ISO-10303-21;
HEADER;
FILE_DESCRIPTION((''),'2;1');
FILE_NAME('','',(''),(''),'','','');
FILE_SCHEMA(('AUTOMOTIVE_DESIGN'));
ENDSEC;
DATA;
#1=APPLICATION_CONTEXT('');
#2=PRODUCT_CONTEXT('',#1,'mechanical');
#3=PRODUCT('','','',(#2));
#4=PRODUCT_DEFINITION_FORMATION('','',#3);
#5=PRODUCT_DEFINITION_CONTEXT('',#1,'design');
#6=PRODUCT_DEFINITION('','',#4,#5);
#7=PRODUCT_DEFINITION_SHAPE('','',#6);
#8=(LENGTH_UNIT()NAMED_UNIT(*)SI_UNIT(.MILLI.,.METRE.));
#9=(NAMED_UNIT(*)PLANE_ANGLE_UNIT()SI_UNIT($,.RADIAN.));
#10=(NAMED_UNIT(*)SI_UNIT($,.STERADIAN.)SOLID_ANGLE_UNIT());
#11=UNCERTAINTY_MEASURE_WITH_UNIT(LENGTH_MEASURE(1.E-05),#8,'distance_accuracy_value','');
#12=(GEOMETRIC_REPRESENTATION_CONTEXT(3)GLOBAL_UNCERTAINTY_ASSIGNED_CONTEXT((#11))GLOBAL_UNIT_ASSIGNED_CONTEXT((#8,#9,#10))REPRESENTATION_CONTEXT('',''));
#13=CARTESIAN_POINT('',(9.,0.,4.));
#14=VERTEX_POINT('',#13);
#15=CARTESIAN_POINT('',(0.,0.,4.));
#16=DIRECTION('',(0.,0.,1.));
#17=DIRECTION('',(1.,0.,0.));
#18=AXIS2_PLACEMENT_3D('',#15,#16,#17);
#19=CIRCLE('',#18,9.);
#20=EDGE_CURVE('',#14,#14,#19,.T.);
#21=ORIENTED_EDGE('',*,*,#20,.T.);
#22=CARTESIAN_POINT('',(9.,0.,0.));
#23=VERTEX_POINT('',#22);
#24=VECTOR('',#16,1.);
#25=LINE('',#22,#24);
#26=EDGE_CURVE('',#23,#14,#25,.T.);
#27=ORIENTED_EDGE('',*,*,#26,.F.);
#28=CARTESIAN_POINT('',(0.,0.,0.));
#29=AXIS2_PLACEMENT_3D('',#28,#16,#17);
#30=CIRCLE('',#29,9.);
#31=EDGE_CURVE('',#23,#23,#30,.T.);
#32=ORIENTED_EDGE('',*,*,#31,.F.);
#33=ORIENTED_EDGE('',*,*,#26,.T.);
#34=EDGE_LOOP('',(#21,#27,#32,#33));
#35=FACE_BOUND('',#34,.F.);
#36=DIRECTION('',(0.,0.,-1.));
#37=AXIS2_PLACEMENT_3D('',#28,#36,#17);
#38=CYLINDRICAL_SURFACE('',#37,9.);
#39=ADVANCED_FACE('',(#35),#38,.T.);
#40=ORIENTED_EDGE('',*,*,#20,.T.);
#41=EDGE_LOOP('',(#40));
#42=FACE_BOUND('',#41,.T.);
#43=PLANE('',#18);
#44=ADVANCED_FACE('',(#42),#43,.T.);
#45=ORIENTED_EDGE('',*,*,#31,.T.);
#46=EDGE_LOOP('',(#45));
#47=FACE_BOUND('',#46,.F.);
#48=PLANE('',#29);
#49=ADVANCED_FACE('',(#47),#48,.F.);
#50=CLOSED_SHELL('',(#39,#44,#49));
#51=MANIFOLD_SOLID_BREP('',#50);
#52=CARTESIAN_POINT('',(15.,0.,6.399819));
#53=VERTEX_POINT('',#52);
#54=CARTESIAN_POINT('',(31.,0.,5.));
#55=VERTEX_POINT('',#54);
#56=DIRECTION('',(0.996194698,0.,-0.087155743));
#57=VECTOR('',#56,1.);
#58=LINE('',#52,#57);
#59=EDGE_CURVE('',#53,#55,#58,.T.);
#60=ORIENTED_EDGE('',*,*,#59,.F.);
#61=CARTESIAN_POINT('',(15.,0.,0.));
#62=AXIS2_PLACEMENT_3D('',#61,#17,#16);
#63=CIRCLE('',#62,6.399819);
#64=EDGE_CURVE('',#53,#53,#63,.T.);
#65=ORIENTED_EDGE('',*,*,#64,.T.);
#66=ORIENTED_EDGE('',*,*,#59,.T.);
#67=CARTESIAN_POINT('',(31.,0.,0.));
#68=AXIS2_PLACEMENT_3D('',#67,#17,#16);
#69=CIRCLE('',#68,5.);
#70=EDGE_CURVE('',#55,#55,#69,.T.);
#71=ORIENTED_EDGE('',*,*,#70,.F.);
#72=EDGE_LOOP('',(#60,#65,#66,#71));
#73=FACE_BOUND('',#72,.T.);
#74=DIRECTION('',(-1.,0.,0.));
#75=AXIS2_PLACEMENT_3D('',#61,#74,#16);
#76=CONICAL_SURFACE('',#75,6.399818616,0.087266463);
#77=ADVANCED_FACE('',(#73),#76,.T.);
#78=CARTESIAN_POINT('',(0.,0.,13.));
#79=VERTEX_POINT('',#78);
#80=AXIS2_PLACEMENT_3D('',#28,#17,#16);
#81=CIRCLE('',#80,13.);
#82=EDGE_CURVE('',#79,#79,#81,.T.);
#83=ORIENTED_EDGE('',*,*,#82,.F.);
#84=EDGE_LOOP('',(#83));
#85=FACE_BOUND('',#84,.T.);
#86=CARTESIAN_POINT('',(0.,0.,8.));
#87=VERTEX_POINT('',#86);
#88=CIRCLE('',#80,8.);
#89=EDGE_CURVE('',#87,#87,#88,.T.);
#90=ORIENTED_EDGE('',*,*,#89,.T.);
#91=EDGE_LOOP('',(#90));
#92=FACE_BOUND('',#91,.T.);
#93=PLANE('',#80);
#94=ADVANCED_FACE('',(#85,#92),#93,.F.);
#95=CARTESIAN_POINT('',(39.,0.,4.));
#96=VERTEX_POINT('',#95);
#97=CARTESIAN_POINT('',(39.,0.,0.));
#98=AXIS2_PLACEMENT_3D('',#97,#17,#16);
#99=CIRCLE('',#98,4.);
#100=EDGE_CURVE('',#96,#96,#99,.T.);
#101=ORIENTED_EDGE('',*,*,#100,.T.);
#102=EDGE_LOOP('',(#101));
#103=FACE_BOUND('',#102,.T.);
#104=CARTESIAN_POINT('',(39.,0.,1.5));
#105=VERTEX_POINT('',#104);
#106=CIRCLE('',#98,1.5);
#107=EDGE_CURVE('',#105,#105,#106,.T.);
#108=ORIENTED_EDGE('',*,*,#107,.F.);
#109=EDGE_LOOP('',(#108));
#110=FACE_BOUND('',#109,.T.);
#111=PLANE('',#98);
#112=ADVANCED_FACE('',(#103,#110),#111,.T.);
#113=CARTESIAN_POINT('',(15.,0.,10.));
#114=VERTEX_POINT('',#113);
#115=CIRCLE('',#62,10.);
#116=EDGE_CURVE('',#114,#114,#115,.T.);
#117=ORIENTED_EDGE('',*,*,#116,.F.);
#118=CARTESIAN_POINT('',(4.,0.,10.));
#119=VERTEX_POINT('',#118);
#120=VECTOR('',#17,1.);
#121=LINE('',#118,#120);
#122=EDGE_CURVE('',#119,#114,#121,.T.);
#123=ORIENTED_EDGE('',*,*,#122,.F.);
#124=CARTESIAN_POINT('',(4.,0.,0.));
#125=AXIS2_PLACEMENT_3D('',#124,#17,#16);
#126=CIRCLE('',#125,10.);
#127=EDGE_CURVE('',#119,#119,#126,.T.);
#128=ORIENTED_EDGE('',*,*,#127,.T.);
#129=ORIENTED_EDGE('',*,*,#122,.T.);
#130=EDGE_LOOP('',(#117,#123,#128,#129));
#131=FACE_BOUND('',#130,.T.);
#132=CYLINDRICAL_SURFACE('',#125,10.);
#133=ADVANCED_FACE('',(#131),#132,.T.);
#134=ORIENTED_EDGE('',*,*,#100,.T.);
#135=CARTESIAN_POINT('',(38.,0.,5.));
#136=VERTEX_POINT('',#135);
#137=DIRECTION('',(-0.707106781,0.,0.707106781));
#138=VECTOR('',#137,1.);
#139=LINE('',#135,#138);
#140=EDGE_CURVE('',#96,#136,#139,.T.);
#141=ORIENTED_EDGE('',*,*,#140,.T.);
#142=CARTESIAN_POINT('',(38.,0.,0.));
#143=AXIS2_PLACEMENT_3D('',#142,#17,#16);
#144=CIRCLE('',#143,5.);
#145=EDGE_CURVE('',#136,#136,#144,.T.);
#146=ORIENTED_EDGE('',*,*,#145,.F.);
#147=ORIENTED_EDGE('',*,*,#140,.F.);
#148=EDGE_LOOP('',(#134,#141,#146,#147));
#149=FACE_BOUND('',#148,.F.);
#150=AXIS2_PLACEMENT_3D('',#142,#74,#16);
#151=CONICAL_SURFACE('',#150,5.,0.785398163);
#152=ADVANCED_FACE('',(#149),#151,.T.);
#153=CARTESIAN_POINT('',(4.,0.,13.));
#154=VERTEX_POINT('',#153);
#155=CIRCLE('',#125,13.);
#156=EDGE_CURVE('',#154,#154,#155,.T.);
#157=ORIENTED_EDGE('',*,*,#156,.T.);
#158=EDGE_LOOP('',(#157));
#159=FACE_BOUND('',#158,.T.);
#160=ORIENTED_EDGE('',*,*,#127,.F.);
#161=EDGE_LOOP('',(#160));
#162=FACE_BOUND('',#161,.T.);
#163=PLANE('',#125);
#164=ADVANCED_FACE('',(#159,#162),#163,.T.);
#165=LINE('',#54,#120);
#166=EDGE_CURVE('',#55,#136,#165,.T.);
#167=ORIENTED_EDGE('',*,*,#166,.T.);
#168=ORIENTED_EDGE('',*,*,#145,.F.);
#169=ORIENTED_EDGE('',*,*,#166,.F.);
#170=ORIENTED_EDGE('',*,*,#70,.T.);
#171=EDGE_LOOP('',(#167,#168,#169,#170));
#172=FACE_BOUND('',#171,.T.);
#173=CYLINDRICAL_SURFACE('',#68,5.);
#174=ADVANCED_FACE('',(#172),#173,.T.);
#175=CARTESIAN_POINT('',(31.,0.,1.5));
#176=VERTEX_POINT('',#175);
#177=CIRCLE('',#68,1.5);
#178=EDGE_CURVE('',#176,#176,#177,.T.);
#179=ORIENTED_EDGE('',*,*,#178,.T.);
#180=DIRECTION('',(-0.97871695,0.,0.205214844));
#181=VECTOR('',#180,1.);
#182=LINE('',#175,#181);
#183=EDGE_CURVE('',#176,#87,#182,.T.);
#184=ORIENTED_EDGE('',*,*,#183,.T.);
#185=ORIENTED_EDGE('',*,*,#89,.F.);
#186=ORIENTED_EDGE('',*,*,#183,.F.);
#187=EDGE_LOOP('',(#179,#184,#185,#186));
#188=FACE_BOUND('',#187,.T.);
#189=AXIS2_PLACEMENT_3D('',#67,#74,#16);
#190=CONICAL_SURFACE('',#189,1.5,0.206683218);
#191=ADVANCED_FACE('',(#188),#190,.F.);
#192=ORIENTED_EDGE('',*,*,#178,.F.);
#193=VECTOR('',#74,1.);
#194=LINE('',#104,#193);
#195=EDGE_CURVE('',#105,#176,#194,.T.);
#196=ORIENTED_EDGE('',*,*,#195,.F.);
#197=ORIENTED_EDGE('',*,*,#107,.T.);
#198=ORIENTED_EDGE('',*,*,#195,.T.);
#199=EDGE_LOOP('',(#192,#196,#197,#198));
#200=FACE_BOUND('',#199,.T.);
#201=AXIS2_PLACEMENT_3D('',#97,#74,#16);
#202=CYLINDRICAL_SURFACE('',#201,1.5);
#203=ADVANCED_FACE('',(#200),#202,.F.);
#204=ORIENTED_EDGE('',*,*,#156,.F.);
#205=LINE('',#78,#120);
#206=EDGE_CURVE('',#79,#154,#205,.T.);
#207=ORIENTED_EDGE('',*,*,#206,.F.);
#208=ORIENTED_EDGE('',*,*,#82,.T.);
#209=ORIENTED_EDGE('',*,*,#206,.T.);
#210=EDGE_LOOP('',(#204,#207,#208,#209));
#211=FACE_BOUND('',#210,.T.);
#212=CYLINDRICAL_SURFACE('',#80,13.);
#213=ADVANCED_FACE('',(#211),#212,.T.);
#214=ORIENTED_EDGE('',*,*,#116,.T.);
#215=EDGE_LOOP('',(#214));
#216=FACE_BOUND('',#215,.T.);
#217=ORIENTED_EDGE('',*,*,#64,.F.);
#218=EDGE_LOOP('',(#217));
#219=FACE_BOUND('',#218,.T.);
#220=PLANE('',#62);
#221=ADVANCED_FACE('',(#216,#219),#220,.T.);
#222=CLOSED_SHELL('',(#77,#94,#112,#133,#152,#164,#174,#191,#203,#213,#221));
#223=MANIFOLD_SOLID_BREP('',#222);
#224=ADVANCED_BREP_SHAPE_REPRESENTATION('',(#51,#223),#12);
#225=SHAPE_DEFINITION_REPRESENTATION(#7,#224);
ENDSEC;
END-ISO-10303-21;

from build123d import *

# Parameters (mm, degrees)
SKETCH8_R           = 9
BOSS_EXTRUDE3_DEPTH = 4
CHAMFER1_SIZE       = 1


with BuildPart() as part:
    # Sketch8 → Boss-Extrude3 (new body)
    with BuildSketch(Plane.XY):
        Circle(SKETCH8_R)
    extrude(amount=BOSS_EXTRUDE3_DEPTH)


with BuildPart() as body_2:
    # Sketch10 → Revolve1 (revolve)
    with BuildSketch(Plane(origin=(0, 0, 0), x_dir=(1, 0, 0), z_dir=(0, 1, 0)), mode=Mode.PRIVATE) as revolve1_sk:
        Polygon((0, 0), (0, 13), (4, 13), (4, 10), (15, 10), (15, 6.399818616), (31, 5), (39, 5), (39, 0), align=None)
    revolve(revolve1_sk.sketch.rotate(Axis((0, 0, 0), (1, 0, 0)), 180), axis=Axis((0, 0, 0), (1, 0, 0)))

    # Sketch11 → Cut-Revolve1 (revolve, cut)
    with BuildSketch(Plane(origin=(0, 0, 0), x_dir=(1, 0, 0), z_dir=(0, 1, 0)), mode=Mode.PRIVATE) as cut_revolve1_sk:
        Polygon((0, 0), (39, 0), (39, 1.5), (31, 1.5), (0, 8), align=None)
    revolve(cut_revolve1_sk.sketch.rotate(Axis((0, 0, 0), (1, 0, 0)), 180), axis=Axis((0, 0, 0), (1, 0, 0)), mode=Mode.SUBTRACT)

    # Chamfer1
    chamfer1_edges = [body_2.edges().sort_by_distance(p)[0] for p in [
        (39, 0, -5),
    ]]
    chamfer(chamfer1_edges, length=CHAMFER1_SIZE)


solid = Compound([part.part, body_2.part])
